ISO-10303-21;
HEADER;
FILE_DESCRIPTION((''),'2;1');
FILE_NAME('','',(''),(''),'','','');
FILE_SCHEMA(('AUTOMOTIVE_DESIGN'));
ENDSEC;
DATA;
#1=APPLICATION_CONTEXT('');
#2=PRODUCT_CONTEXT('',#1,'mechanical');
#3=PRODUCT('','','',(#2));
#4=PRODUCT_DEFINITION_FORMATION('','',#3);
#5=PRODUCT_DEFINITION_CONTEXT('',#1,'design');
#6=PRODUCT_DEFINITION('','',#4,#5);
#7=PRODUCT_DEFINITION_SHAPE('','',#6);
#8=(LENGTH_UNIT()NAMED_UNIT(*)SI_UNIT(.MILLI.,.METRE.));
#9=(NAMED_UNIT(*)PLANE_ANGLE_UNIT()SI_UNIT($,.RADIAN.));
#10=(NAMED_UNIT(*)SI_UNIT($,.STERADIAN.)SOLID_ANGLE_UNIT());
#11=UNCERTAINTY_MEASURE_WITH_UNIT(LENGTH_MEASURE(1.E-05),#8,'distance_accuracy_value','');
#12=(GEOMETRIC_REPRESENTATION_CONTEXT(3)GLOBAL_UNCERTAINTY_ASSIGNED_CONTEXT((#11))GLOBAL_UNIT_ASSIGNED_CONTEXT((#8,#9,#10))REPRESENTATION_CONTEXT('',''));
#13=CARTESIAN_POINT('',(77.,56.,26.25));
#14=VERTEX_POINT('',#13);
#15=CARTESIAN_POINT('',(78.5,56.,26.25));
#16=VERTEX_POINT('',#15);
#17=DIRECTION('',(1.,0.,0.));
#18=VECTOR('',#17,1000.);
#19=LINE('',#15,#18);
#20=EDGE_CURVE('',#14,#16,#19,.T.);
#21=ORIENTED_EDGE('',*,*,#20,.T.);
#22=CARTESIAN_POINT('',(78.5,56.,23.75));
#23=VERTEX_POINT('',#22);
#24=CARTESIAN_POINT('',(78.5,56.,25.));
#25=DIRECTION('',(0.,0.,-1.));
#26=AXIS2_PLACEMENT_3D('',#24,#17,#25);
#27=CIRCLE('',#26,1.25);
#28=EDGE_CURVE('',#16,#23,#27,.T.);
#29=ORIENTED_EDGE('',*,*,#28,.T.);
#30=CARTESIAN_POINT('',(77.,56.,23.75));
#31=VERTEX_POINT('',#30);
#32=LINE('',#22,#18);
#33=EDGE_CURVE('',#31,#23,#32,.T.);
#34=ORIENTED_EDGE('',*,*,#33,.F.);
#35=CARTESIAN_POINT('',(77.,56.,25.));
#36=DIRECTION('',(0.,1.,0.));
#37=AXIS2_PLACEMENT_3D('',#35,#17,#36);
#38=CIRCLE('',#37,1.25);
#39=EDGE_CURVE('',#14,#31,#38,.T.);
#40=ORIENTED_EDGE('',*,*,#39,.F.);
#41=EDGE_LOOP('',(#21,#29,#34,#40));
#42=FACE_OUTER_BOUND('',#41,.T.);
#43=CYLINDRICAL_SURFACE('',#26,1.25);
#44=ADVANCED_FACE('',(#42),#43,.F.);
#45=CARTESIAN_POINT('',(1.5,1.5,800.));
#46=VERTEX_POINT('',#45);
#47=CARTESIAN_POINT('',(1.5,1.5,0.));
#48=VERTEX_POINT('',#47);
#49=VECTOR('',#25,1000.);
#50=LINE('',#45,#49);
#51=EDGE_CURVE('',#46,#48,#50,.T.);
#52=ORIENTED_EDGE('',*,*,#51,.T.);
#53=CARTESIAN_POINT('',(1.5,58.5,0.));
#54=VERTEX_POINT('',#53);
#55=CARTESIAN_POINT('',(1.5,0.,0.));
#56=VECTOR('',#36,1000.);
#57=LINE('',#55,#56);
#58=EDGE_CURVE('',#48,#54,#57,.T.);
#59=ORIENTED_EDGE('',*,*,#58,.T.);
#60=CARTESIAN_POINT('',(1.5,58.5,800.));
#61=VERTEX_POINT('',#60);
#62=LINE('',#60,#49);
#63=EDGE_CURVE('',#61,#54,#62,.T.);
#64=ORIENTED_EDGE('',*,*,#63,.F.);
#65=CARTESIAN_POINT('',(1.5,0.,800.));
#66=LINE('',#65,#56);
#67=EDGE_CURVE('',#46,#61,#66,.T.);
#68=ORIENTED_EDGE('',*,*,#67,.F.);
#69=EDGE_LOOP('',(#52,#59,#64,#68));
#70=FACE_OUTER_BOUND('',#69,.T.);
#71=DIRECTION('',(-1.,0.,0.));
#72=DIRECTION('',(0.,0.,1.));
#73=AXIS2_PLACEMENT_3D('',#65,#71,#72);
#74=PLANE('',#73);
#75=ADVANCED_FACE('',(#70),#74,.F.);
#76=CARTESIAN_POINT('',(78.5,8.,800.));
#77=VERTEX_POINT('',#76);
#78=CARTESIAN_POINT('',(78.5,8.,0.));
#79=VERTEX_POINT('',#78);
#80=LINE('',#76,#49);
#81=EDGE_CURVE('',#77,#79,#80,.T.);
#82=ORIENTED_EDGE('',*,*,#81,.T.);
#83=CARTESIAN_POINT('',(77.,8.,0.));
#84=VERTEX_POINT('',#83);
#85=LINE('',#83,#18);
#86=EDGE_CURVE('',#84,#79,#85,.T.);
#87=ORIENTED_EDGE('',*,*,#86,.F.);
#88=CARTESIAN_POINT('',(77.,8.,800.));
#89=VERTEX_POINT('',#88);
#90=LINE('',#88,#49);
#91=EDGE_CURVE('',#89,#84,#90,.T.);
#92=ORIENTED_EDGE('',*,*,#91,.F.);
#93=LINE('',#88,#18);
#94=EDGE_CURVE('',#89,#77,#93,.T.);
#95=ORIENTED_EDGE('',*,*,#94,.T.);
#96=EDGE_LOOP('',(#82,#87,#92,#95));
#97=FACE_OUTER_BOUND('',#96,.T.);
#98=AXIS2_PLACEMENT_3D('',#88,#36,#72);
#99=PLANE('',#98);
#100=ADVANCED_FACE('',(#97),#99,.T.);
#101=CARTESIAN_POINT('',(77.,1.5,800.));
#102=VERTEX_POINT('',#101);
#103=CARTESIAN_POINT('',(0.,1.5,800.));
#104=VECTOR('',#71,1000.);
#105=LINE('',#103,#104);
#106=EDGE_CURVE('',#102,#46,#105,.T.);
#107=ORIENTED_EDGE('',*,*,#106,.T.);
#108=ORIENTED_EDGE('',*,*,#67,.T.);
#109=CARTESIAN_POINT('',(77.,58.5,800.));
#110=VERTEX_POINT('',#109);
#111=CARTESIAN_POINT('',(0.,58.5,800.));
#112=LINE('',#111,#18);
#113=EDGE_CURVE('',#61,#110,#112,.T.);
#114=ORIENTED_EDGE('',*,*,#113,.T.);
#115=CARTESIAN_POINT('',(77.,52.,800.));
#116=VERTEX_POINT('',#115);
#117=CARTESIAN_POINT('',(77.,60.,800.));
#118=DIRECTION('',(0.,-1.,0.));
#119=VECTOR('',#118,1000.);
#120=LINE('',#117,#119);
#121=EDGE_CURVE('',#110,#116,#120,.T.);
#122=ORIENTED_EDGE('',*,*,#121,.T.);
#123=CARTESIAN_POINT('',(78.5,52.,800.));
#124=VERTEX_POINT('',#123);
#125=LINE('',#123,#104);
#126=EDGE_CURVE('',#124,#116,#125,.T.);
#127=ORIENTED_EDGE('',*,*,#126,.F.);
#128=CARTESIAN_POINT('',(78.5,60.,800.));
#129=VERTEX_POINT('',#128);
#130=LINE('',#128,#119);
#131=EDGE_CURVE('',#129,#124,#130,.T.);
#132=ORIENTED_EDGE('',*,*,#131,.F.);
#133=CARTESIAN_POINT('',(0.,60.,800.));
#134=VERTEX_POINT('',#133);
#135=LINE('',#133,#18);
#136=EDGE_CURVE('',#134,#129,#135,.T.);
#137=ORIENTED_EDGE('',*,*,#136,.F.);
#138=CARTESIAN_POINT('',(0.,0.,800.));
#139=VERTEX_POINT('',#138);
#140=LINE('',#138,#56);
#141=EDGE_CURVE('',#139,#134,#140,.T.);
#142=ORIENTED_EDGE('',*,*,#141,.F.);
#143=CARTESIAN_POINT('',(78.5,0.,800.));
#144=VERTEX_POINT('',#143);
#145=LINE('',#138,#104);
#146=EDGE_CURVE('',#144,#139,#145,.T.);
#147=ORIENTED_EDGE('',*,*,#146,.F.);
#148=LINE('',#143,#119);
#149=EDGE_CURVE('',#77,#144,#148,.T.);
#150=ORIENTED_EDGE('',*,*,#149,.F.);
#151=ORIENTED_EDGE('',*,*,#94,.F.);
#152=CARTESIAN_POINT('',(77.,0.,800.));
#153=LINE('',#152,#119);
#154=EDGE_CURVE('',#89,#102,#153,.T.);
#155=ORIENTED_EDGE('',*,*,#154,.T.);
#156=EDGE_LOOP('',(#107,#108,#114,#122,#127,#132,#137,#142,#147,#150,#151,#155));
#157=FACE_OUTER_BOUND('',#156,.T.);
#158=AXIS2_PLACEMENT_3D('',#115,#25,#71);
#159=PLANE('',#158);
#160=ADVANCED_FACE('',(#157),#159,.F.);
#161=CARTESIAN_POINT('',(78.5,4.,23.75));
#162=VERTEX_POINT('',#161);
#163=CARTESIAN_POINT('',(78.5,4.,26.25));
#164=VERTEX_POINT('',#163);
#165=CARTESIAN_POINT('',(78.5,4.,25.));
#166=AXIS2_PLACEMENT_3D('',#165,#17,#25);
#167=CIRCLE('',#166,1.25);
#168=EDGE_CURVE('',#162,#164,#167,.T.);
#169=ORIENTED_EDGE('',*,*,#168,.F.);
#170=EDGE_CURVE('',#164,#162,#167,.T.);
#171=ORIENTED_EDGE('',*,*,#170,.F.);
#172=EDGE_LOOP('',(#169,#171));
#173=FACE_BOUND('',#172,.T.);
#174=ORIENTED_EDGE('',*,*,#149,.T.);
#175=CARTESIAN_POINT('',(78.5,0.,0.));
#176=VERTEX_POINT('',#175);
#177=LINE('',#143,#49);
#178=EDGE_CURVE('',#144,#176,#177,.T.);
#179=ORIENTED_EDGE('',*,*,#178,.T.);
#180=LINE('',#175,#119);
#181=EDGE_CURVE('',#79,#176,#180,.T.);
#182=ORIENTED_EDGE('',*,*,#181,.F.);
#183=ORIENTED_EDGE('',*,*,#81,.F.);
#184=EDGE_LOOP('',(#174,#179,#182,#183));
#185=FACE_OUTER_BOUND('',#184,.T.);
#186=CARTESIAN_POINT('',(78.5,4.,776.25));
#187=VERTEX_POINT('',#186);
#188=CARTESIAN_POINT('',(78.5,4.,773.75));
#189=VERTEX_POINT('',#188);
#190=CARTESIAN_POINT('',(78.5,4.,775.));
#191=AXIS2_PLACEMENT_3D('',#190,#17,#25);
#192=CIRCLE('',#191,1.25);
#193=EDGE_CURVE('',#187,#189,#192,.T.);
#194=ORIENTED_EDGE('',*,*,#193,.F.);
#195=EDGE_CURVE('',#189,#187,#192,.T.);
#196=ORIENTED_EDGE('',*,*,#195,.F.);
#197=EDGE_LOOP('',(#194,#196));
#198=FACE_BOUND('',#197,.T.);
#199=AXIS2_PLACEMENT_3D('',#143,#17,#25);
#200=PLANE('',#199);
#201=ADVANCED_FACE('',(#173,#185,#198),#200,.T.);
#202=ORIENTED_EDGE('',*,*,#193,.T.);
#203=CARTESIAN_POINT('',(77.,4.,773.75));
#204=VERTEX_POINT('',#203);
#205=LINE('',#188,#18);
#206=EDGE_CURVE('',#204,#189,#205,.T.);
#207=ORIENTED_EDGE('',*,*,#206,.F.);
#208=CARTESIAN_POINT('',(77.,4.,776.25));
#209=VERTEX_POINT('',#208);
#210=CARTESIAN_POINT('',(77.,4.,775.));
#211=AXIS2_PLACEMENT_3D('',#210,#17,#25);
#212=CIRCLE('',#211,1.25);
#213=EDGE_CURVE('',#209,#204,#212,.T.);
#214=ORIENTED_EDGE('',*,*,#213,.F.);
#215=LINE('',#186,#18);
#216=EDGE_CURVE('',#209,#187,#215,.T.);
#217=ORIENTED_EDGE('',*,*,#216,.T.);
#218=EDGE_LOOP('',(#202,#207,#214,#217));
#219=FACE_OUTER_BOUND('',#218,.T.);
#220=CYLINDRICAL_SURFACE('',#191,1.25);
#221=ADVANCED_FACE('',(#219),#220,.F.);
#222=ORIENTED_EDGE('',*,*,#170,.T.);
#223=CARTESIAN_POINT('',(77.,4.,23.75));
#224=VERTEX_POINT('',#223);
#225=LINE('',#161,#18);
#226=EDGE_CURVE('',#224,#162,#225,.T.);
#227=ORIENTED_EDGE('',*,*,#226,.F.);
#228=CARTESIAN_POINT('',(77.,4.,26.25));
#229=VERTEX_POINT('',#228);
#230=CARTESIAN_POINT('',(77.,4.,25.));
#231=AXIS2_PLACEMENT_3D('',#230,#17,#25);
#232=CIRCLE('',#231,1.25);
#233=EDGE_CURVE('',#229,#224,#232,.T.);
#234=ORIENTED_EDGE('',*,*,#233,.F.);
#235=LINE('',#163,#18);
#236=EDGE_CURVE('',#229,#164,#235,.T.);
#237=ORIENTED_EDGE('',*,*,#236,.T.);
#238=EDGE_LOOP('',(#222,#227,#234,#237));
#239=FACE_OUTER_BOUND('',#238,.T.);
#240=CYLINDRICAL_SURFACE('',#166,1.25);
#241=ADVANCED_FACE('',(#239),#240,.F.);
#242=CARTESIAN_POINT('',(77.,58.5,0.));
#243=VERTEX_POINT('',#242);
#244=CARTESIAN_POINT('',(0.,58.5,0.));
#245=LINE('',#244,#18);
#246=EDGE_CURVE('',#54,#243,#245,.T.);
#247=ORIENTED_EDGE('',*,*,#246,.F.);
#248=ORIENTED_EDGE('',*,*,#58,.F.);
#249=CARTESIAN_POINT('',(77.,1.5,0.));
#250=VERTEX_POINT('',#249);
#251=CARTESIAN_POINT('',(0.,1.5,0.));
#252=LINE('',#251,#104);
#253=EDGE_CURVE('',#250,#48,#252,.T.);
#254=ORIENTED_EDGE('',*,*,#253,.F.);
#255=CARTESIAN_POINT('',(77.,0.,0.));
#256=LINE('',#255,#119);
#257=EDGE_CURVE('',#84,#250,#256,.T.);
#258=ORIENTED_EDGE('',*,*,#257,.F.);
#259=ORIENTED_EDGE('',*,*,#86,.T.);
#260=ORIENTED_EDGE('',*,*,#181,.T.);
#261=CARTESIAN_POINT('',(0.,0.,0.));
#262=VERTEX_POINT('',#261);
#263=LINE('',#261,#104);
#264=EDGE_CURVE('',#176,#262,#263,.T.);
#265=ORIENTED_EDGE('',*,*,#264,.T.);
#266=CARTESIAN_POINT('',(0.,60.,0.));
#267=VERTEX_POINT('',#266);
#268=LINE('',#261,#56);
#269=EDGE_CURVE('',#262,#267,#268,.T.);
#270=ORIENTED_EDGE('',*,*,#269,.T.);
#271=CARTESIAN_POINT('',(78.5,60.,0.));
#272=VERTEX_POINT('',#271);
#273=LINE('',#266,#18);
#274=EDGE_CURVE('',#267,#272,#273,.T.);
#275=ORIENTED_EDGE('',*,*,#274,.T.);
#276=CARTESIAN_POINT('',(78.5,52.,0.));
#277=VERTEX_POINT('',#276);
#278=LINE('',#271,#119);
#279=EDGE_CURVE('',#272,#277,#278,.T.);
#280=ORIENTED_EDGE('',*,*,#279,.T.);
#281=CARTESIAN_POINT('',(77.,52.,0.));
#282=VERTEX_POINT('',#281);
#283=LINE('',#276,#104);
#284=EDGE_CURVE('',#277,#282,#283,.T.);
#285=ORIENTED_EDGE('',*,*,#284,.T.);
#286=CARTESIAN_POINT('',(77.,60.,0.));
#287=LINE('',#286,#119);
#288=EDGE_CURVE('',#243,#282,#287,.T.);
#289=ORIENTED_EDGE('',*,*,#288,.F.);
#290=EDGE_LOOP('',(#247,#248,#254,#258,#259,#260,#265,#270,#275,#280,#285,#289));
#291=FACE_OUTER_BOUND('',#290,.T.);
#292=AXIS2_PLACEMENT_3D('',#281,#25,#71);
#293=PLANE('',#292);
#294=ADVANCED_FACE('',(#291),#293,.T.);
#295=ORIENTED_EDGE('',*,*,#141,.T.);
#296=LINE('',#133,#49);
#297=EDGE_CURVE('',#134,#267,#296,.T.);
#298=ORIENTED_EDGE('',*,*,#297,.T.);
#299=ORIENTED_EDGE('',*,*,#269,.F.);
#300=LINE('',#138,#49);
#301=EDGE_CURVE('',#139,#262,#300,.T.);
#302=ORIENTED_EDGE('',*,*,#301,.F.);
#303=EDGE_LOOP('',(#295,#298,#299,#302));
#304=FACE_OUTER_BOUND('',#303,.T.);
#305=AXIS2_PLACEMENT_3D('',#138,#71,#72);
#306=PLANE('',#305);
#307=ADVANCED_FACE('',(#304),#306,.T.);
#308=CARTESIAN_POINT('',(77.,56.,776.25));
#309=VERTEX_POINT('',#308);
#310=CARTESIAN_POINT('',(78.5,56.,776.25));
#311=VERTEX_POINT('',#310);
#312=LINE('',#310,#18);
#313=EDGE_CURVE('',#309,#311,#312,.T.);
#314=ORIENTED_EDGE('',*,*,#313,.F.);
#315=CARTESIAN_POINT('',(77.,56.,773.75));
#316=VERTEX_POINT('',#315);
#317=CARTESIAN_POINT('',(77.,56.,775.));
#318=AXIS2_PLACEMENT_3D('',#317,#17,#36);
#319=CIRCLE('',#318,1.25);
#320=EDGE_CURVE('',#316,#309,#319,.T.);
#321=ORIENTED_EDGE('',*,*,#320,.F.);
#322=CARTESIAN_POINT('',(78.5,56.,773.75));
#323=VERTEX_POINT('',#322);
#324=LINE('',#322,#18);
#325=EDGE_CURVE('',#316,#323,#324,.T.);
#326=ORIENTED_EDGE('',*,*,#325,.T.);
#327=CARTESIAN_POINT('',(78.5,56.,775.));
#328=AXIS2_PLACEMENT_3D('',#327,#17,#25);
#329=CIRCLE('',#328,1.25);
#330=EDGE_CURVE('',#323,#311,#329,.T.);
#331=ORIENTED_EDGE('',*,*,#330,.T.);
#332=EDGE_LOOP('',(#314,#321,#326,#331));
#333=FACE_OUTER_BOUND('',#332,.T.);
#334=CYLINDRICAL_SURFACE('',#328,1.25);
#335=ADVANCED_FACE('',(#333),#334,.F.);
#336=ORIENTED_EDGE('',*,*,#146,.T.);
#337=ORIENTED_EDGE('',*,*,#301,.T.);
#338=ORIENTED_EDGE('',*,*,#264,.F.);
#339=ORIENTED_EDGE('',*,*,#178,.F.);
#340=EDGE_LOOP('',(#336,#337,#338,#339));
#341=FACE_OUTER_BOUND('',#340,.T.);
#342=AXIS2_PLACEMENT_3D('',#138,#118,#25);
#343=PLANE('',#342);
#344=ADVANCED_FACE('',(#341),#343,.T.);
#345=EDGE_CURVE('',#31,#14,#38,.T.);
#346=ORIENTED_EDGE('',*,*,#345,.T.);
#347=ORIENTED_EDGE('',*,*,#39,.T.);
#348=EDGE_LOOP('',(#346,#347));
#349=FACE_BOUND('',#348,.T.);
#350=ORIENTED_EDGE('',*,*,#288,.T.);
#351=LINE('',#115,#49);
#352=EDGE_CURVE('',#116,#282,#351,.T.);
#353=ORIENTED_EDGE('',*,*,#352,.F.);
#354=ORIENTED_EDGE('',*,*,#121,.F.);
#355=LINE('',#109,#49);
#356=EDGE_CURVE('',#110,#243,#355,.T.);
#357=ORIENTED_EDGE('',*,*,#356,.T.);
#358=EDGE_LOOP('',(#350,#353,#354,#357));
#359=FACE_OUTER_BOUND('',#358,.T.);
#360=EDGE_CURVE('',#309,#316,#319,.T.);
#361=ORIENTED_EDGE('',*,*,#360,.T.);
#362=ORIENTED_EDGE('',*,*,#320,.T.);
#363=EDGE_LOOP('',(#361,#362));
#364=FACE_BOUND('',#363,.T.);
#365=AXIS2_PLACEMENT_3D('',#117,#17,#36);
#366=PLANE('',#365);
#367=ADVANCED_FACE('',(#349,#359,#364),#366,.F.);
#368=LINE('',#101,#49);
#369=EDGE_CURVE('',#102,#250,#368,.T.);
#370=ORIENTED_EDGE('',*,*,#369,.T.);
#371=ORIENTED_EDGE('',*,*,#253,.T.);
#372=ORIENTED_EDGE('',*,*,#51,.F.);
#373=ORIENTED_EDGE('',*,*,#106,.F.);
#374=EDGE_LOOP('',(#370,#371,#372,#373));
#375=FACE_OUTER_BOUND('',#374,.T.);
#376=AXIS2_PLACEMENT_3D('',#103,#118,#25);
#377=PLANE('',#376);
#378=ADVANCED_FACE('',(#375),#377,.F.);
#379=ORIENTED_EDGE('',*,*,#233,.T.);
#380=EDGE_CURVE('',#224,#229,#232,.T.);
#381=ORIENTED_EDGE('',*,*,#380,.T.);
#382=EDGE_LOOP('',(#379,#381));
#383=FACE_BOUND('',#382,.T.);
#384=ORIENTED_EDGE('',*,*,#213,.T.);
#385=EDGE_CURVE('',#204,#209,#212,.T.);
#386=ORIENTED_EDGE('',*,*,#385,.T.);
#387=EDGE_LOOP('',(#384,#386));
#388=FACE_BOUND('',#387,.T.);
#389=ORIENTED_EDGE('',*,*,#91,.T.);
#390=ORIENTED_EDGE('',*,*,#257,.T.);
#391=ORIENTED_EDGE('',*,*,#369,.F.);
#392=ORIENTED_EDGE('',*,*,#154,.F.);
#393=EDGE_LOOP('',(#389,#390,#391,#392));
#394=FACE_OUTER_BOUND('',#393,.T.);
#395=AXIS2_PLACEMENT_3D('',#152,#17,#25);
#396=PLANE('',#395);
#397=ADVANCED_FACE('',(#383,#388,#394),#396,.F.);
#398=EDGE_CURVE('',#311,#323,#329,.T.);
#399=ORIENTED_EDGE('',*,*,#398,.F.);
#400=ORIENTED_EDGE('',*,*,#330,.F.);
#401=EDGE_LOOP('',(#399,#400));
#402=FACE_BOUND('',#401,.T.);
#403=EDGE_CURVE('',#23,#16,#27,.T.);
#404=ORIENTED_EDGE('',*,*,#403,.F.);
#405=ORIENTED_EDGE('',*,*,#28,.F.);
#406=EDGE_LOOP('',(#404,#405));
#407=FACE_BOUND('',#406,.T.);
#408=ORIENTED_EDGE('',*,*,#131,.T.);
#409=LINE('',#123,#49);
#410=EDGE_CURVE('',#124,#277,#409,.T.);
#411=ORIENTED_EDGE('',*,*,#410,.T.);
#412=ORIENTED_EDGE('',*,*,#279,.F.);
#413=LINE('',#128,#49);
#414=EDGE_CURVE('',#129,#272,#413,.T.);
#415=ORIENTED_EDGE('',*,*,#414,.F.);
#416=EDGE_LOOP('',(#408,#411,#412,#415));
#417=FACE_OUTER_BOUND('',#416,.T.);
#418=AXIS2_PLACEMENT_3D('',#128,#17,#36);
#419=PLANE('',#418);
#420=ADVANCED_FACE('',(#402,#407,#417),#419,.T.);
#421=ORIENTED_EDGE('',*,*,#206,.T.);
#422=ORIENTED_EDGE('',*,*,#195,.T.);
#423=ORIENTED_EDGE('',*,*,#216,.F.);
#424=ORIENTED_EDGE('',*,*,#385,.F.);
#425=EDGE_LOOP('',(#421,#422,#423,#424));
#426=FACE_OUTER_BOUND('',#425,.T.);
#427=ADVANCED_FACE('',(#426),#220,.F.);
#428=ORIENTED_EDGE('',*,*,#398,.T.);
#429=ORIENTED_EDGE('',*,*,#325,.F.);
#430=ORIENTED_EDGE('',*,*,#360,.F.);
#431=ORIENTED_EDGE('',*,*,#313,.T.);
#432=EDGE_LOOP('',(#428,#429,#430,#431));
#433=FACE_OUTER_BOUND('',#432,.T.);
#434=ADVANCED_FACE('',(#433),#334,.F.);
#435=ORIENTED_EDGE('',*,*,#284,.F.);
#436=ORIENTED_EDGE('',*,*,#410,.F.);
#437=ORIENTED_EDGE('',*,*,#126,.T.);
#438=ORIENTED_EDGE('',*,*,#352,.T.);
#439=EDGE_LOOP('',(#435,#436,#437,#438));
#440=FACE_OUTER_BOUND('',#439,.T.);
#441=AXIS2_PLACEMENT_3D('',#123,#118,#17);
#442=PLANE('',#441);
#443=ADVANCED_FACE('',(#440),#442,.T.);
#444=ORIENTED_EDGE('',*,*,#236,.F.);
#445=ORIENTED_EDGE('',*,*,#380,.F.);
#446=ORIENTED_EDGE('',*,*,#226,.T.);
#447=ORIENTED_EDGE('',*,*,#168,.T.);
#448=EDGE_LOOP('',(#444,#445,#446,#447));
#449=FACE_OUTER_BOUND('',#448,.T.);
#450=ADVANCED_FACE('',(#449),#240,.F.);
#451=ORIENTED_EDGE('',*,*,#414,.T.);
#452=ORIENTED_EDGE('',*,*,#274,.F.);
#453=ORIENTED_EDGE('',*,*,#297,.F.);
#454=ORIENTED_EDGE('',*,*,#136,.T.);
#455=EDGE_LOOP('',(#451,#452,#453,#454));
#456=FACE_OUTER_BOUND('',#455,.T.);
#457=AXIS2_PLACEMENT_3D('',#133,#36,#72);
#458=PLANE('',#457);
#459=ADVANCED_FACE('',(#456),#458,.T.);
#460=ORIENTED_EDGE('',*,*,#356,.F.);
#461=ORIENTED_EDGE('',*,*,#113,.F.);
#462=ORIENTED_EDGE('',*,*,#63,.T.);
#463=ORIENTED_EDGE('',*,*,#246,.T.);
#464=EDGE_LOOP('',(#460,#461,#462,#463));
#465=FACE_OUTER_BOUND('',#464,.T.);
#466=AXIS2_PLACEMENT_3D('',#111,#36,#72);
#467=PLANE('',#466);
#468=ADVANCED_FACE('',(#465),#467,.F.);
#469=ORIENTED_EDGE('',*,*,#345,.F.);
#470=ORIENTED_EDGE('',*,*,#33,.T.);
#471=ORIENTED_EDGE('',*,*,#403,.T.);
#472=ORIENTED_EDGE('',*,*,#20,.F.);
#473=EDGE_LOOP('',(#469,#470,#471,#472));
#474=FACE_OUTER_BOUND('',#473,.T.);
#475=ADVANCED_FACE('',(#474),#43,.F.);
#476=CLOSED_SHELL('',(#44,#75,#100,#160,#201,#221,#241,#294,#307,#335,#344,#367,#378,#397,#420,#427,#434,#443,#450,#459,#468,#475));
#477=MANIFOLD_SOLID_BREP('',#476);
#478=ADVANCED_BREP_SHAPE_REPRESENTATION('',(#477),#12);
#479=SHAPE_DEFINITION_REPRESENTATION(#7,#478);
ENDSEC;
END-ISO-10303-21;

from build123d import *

# Parameters (mm, degrees)
EXTRUDE_1_DEPTH         = 800
HOLE_WIZARD_M3_1_REACH  = 808.078
HOLE_WIZARD_M3_1_BORE_R = 1.25


with BuildPart() as part:
    # 草图1 → 拉伸-薄壁1 (new body)
    with BuildSketch(Plane.XY):
        Polygon((78.5, 52), (78.5, 60), (0, 60), (0, 0), (78.5, 0), (78.5, 8), (77, 8), (77, 1.5), (1.5, 1.5), (1.5, 58.5), (77, 58.5), (77, 52), align=None)
    extrude(amount=EXTRUDE_1_DEPTH)

    # M3 螺纹孔1 bore → M3 螺纹孔1 (cut, up to next)
    with BuildSketch(Plane(origin=(78.5, 0, 0), x_dir=(0, 0, -1), z_dir=(1, 0, 0)), mode=Mode.PRIVATE) as hole_wizard_m3_1_sk1:
        with Locations((-775, 56)):
            Circle(HOLE_WIZARD_M3_1_BORE_R)
    hole_wizard_m3_1_tool1 = extrude(hole_wizard_m3_1_sk1.sketch, amount=-HOLE_WIZARD_M3_1_REACH, mode=Mode.PRIVATE) & part.part
    # M3 螺纹孔1 bore → M3 螺纹孔1 (cut, up to next)
    with BuildSketch(Plane(origin=(78.5, 0, 0), x_dir=(0, 0, -1), z_dir=(1, 0, 0)), mode=Mode.PRIVATE) as hole_wizard_m3_1_sk2:
        with Locations((-25, 56)):
            Circle(HOLE_WIZARD_M3_1_BORE_R)
    hole_wizard_m3_1_tool2 = extrude(hole_wizard_m3_1_sk2.sketch, amount=-HOLE_WIZARD_M3_1_REACH, mode=Mode.PRIVATE) & part.part
    hole_wizard_m3_1_1 = hole_wizard_m3_1_tool1.solids().sort_by_distance((78.5, 56, 775))[0]
    add(hole_wizard_m3_1_1, mode=Mode.SUBTRACT)
    hole_wizard_m3_1_2 = hole_wizard_m3_1_tool2.solids().sort_by_distance((78.5, 56, 25))[0]
    add(hole_wizard_m3_1_2, mode=Mode.SUBTRACT)
    hole_wizard_m3_1 = hole_wizard_m3_1_1 + hole_wizard_m3_1_2  # M3 螺纹孔1 as one shape, for the pattern or mirror that repeats it

    # 镜向2: M3 螺纹孔1 across plane
    add(hole_wizard_m3_1.mirror(Plane(origin=(0, 30, 0), x_dir=(0, 0, 1), z_dir=(0, -1, 0))), mode=Mode.SUBTRACT)


solid = part.part
